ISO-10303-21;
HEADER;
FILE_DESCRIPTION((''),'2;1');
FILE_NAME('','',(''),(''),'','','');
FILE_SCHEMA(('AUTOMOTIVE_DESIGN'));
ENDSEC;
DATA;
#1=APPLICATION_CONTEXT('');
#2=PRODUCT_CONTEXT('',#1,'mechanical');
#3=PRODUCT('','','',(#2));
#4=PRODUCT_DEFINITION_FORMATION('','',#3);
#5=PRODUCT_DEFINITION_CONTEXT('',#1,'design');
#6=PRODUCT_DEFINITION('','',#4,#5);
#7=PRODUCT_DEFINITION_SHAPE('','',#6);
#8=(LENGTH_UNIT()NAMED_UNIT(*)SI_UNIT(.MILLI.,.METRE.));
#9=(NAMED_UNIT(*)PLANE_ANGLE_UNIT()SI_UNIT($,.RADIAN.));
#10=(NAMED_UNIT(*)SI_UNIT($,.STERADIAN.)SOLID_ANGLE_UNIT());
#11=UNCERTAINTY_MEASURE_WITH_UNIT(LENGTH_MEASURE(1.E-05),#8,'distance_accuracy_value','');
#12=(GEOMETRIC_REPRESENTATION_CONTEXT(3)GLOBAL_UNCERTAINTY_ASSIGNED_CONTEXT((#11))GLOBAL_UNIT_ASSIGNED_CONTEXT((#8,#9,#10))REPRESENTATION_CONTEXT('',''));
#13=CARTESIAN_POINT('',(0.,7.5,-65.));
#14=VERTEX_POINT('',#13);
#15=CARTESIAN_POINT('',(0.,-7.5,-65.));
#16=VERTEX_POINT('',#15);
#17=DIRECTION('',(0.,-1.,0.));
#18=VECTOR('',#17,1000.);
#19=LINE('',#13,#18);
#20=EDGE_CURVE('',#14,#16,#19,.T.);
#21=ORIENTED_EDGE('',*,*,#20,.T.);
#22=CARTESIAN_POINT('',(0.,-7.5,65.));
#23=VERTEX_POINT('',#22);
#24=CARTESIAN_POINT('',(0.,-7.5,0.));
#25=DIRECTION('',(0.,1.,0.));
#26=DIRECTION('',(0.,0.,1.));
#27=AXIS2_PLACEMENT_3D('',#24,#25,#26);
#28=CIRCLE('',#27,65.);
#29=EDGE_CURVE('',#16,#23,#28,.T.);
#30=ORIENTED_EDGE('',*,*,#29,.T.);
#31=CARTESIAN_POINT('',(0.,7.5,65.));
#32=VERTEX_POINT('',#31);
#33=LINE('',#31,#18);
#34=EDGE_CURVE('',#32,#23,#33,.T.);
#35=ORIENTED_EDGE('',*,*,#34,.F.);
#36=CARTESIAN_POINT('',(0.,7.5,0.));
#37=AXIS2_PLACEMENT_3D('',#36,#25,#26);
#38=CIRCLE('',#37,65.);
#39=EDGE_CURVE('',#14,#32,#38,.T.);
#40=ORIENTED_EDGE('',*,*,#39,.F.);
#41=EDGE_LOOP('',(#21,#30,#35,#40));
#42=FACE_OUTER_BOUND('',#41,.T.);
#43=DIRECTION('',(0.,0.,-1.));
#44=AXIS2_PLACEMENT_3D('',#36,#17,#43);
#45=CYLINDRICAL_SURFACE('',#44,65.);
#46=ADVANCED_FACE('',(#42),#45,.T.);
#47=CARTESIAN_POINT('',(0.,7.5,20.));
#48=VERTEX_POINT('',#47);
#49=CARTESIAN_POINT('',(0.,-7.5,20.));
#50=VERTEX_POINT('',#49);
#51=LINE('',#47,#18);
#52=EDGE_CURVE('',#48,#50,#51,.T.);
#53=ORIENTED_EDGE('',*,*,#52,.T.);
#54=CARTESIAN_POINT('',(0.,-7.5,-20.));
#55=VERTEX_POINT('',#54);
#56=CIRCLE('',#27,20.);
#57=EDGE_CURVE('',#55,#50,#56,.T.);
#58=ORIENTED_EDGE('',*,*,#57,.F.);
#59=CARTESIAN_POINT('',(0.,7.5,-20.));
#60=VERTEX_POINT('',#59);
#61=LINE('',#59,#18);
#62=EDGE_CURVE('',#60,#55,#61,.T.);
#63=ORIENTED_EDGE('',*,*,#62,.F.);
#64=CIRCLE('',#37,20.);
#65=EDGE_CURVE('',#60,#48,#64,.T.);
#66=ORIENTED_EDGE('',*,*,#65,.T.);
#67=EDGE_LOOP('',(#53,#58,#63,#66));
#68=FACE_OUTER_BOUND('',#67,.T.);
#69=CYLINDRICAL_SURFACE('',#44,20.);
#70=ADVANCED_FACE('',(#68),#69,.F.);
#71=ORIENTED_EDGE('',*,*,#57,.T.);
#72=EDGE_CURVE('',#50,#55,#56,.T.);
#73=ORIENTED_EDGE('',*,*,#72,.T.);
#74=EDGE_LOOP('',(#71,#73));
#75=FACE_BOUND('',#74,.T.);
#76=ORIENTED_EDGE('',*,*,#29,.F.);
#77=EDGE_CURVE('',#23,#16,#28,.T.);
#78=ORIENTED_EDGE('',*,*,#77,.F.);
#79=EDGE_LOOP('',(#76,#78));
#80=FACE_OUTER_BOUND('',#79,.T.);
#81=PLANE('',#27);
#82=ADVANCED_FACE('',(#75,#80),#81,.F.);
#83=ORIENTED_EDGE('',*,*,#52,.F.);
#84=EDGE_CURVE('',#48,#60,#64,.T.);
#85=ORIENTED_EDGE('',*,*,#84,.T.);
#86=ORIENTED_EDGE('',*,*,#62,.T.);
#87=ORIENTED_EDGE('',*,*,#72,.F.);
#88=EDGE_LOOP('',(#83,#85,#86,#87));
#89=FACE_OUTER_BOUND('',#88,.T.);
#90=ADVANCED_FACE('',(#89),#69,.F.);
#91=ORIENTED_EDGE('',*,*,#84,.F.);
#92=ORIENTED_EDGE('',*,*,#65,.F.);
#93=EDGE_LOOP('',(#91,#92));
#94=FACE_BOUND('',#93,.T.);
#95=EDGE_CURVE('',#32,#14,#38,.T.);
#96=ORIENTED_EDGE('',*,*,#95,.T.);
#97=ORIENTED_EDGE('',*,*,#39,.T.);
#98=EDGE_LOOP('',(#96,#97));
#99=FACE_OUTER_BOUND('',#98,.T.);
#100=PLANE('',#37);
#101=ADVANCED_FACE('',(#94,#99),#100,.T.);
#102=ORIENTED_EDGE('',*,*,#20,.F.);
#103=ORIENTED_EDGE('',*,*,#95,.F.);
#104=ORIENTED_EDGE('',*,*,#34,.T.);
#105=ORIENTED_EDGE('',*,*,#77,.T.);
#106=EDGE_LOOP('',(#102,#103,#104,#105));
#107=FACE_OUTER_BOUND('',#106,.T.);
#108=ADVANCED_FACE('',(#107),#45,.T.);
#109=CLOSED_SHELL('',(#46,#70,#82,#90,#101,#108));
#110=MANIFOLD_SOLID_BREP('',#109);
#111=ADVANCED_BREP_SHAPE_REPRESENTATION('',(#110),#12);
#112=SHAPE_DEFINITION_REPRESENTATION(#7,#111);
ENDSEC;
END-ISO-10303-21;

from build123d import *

# Parameters (mm, degrees)
SKETCH_1_R      = 65
SKETCH_1_R_2    = 20
EXTRUDE_1_DEPTH = 7.5


with BuildPart() as part:
    # 草图1 → 凸台-拉伸1 (new, symmetric)
    with BuildSketch(Plane(origin=(0, 0, 0), x_dir=(1, 0, 0), z_dir=(0, 1, 0))):
        with Locations(Location((0, 0, 0), (0, 0, 270))):
            Circle(SKETCH_1_R)
        with Locations(Location((0, 0, 0), (0, 0, 270))):
            Circle(SKETCH_1_R_2, mode=Mode.SUBTRACT)
    extrude(amount=EXTRUDE_1_DEPTH, both=True)


solid = part.part
